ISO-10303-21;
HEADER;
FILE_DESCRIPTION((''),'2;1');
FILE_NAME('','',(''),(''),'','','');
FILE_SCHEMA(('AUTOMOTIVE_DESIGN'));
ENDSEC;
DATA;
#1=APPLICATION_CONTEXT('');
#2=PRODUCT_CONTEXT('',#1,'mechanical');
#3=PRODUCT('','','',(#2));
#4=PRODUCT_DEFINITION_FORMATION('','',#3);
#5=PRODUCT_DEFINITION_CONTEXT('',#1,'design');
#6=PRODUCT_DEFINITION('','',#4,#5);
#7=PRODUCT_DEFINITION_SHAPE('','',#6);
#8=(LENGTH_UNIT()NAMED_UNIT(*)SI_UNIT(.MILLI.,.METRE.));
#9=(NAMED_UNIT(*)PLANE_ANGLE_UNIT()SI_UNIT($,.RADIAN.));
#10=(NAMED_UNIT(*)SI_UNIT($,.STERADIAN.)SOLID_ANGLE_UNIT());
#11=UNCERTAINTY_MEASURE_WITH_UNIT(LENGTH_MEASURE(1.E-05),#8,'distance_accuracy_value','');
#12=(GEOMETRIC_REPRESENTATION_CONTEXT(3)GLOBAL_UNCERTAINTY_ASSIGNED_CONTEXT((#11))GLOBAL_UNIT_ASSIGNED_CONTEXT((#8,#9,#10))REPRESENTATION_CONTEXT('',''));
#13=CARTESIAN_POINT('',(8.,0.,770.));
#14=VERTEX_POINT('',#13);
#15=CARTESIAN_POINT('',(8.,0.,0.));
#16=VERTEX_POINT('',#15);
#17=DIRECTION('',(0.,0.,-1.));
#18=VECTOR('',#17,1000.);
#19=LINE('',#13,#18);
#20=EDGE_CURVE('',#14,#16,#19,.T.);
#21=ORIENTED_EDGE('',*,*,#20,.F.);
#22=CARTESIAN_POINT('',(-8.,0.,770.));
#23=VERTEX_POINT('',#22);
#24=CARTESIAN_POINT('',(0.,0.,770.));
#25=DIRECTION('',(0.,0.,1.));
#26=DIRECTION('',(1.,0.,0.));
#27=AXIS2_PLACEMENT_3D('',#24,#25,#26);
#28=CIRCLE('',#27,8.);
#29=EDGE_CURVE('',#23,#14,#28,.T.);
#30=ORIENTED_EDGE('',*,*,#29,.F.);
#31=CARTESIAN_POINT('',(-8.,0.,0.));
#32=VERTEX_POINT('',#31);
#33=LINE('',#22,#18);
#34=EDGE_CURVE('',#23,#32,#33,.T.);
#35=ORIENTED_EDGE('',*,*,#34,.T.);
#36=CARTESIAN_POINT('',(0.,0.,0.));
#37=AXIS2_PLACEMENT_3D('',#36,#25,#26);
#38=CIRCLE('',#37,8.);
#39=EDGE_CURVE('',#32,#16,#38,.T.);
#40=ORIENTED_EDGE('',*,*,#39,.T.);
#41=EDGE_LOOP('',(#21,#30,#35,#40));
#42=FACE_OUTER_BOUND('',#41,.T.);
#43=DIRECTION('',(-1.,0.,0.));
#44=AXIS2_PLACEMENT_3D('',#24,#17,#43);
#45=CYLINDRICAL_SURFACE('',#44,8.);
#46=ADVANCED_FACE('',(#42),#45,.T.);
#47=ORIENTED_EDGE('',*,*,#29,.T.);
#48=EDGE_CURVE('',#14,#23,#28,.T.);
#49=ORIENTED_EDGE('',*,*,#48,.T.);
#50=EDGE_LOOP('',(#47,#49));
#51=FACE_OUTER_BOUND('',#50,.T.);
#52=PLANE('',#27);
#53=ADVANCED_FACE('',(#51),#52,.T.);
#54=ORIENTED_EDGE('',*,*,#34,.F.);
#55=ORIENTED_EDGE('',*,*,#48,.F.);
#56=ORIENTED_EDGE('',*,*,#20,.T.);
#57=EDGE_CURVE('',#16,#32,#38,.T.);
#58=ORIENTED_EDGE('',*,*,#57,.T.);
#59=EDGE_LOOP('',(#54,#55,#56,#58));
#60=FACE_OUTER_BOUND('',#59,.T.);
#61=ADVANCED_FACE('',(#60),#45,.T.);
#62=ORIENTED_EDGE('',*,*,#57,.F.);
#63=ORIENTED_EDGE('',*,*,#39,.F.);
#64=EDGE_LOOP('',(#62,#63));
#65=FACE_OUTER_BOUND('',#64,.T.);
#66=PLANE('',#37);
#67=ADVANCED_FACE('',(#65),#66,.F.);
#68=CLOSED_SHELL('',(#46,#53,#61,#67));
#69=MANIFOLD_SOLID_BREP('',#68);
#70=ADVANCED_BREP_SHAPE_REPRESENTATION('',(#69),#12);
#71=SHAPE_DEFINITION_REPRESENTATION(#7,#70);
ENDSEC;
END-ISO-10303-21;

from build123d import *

# Parameters (mm, degrees)
SKETCH_1_R        = 8
EXTRUDE_207_DEPTH = 770


with BuildPart() as part:
    # 草图1 → Extrude 207 (new body)
    with BuildSketch(Plane.XY):
        Circle(SKETCH_1_R)
    extrude(amount=EXTRUDE_207_DEPTH)


solid = part.part
